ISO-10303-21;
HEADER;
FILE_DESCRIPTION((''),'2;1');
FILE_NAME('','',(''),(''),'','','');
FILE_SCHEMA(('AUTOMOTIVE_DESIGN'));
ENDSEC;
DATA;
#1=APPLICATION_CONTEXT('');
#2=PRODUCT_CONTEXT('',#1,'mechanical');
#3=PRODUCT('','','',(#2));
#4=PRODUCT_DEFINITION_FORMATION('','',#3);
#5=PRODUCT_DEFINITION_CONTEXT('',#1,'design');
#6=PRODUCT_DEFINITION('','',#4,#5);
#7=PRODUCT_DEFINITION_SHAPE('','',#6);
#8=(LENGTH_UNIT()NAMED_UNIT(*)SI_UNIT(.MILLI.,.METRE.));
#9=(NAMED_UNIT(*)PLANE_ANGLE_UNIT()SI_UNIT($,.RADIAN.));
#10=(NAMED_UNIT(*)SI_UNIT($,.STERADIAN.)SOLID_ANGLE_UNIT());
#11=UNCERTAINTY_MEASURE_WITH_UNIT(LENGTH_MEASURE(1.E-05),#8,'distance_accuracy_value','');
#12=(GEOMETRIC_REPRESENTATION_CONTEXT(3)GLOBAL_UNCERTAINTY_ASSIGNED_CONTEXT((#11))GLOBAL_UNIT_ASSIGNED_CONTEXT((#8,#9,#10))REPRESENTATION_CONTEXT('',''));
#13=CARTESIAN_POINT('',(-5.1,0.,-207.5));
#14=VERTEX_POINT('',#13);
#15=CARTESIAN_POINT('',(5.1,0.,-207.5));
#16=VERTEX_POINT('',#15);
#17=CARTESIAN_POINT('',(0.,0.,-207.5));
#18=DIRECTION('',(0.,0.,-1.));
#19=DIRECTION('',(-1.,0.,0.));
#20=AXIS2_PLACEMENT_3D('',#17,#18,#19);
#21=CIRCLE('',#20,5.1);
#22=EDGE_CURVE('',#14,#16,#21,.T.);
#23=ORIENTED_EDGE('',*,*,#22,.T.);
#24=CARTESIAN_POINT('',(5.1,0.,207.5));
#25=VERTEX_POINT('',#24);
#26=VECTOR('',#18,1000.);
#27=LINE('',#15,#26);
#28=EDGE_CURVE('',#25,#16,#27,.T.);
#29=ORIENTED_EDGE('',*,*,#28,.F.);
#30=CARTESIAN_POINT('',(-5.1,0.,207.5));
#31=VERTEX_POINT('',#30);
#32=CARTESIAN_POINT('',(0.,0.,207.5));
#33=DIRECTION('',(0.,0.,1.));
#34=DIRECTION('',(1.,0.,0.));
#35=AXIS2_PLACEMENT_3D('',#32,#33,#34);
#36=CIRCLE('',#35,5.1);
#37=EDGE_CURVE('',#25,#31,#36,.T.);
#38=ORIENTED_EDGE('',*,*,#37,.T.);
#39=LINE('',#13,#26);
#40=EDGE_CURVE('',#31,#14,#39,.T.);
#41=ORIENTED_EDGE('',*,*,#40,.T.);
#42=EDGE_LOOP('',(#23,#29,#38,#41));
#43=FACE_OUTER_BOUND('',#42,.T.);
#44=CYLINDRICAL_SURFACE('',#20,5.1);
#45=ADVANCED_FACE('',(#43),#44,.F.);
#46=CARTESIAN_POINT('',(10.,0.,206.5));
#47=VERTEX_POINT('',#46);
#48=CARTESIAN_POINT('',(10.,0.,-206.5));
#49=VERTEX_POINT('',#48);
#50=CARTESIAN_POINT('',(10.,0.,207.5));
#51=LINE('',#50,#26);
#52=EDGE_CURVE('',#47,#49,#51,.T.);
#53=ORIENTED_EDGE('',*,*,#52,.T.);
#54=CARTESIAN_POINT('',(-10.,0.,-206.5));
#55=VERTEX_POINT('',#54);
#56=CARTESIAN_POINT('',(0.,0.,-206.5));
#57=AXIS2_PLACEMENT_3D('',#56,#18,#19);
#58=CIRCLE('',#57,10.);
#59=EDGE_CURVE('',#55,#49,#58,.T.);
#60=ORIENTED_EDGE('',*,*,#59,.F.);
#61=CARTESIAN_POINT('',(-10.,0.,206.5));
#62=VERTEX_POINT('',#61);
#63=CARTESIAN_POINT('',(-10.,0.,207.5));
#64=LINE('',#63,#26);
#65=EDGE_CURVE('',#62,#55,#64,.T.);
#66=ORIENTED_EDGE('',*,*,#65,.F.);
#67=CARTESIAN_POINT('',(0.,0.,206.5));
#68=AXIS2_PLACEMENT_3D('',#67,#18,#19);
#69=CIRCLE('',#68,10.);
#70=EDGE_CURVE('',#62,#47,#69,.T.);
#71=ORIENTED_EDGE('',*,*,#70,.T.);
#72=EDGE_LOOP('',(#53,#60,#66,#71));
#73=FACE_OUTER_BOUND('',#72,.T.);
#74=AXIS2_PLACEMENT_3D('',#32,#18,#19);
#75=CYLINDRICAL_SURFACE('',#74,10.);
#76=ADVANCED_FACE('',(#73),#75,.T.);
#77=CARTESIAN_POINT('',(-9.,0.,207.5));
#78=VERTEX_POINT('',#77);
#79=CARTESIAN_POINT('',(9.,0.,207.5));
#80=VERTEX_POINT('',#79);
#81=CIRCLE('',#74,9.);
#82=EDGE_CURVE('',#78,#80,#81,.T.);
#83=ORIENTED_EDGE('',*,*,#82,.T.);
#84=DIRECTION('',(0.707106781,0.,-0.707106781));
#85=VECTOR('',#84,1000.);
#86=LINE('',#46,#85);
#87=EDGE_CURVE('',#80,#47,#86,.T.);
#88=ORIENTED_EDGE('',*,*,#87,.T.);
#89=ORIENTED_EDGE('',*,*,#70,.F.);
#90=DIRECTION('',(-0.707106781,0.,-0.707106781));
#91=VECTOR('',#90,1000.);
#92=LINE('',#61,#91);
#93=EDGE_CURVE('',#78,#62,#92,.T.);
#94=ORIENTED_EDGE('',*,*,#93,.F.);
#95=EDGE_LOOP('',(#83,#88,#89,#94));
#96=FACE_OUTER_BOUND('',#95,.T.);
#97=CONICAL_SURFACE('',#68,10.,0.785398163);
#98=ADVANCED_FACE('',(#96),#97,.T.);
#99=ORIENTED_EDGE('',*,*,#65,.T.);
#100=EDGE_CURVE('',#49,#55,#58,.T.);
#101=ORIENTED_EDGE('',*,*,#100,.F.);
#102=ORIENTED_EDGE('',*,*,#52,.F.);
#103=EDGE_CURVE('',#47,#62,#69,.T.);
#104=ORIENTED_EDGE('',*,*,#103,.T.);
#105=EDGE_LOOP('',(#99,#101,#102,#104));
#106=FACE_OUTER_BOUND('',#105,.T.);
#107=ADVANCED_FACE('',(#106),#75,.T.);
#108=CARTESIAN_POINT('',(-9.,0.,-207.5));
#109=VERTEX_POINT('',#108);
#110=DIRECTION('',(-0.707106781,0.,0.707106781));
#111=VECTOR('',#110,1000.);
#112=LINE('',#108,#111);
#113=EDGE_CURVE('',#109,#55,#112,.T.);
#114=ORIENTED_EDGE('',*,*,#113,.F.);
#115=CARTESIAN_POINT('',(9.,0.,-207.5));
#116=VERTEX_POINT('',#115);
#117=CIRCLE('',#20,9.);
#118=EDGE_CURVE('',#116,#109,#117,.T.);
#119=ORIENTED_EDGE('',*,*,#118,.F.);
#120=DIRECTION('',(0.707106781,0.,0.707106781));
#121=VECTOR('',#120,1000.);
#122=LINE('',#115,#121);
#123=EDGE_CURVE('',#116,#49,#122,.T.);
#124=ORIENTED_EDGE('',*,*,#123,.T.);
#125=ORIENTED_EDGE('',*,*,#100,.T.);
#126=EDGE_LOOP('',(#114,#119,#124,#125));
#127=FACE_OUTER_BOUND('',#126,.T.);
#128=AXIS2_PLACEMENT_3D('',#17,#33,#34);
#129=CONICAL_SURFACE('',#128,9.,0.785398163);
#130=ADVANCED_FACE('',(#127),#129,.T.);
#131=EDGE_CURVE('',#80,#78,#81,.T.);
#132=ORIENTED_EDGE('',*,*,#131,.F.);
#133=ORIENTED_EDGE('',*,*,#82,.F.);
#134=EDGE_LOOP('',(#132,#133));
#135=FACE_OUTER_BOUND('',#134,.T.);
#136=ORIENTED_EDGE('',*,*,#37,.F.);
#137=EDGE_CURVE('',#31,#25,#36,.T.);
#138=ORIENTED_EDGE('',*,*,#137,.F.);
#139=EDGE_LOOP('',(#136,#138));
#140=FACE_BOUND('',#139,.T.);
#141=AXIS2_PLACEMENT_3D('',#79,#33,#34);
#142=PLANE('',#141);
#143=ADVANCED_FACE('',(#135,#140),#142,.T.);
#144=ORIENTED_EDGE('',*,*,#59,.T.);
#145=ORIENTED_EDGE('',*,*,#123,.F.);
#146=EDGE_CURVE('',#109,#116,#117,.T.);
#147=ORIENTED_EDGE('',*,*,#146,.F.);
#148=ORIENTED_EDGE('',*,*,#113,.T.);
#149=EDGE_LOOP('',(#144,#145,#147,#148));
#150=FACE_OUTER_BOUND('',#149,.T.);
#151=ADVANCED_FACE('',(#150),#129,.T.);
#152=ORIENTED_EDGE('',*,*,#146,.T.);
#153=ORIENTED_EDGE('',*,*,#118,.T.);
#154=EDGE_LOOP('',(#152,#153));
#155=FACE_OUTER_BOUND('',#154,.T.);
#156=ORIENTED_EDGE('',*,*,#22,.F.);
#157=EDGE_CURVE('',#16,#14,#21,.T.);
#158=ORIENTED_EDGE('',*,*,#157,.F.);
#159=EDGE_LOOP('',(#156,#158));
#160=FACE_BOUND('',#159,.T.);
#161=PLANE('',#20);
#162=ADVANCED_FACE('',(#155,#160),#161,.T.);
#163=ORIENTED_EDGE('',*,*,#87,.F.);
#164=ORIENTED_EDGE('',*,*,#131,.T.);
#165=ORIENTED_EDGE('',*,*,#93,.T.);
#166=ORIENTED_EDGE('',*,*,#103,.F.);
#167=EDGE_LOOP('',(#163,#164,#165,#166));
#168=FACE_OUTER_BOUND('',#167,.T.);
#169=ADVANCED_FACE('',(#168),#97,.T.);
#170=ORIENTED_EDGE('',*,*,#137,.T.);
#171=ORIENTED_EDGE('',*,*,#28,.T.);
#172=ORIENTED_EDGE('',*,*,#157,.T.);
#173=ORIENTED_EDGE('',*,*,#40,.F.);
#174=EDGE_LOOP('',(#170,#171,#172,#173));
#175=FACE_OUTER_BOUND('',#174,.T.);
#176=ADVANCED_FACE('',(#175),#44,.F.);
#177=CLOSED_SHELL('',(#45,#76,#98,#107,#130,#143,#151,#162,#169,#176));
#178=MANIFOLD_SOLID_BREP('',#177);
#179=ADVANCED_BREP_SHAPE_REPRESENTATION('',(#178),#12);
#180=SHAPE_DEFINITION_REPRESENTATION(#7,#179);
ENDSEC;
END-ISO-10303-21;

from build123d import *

# Parameters (mm, degrees)
HOLE_WIZARD_M12_5_D     = 10.2
HOLE_WIZARD_M12_5_DEPTH = 220
HOLE_WIZARD_M12_5_TIP   = 3.064389157
HOLE_WIZARD_M12_6_D     = 10.2
HOLE_WIZARD_M12_6_DEPTH = 220
HOLE_WIZARD_M12_6_TIP   = 3.064389157


with BuildPart() as part:
    # 草图1 → 旋转1 (revolve)
    with BuildSketch(Plane.XZ, mode=Mode.PRIVATE) as revolve_1_sk:
        Polygon((9, -207.5), (10, -206.5), (10, 206.5), (9, 207.5), (0, 207.5), (0, -207.5), align=None)
    revolve(revolve_1_sk.sketch.rotate(Axis((0, 0, 207.5), (0, 0, -1)), 180), axis=Axis((0, 0, 207.5), (0, 0, -1)))

    # M12 螺纹孔5
    with Locations(Plane(origin=(0, 0, -207.5), x_dir=(-1, 0, 0), z_dir=(0, 0, -1))):
        with Locations((0, 0)):
            Hole(HOLE_WIZARD_M12_5_D / 2, depth=HOLE_WIZARD_M12_5_DEPTH)
            with Locations((0, 0, -(HOLE_WIZARD_M12_5_DEPTH + HOLE_WIZARD_M12_5_TIP / 2))):  # 118° drill point
                Cone(0, HOLE_WIZARD_M12_5_D / 2, HOLE_WIZARD_M12_5_TIP, mode=Mode.SUBTRACT)

    # M12 螺纹孔6
    with Locations(Plane.XY.offset(207.5)):
        with Locations((0, 0)):
            Hole(HOLE_WIZARD_M12_6_D / 2, depth=HOLE_WIZARD_M12_6_DEPTH)
            with Locations((0, 0, -(HOLE_WIZARD_M12_6_DEPTH + HOLE_WIZARD_M12_6_TIP / 2))):  # 118° drill point
                Cone(0, HOLE_WIZARD_M12_6_D / 2, HOLE_WIZARD_M12_6_TIP, mode=Mode.SUBTRACT)


solid = part.part
